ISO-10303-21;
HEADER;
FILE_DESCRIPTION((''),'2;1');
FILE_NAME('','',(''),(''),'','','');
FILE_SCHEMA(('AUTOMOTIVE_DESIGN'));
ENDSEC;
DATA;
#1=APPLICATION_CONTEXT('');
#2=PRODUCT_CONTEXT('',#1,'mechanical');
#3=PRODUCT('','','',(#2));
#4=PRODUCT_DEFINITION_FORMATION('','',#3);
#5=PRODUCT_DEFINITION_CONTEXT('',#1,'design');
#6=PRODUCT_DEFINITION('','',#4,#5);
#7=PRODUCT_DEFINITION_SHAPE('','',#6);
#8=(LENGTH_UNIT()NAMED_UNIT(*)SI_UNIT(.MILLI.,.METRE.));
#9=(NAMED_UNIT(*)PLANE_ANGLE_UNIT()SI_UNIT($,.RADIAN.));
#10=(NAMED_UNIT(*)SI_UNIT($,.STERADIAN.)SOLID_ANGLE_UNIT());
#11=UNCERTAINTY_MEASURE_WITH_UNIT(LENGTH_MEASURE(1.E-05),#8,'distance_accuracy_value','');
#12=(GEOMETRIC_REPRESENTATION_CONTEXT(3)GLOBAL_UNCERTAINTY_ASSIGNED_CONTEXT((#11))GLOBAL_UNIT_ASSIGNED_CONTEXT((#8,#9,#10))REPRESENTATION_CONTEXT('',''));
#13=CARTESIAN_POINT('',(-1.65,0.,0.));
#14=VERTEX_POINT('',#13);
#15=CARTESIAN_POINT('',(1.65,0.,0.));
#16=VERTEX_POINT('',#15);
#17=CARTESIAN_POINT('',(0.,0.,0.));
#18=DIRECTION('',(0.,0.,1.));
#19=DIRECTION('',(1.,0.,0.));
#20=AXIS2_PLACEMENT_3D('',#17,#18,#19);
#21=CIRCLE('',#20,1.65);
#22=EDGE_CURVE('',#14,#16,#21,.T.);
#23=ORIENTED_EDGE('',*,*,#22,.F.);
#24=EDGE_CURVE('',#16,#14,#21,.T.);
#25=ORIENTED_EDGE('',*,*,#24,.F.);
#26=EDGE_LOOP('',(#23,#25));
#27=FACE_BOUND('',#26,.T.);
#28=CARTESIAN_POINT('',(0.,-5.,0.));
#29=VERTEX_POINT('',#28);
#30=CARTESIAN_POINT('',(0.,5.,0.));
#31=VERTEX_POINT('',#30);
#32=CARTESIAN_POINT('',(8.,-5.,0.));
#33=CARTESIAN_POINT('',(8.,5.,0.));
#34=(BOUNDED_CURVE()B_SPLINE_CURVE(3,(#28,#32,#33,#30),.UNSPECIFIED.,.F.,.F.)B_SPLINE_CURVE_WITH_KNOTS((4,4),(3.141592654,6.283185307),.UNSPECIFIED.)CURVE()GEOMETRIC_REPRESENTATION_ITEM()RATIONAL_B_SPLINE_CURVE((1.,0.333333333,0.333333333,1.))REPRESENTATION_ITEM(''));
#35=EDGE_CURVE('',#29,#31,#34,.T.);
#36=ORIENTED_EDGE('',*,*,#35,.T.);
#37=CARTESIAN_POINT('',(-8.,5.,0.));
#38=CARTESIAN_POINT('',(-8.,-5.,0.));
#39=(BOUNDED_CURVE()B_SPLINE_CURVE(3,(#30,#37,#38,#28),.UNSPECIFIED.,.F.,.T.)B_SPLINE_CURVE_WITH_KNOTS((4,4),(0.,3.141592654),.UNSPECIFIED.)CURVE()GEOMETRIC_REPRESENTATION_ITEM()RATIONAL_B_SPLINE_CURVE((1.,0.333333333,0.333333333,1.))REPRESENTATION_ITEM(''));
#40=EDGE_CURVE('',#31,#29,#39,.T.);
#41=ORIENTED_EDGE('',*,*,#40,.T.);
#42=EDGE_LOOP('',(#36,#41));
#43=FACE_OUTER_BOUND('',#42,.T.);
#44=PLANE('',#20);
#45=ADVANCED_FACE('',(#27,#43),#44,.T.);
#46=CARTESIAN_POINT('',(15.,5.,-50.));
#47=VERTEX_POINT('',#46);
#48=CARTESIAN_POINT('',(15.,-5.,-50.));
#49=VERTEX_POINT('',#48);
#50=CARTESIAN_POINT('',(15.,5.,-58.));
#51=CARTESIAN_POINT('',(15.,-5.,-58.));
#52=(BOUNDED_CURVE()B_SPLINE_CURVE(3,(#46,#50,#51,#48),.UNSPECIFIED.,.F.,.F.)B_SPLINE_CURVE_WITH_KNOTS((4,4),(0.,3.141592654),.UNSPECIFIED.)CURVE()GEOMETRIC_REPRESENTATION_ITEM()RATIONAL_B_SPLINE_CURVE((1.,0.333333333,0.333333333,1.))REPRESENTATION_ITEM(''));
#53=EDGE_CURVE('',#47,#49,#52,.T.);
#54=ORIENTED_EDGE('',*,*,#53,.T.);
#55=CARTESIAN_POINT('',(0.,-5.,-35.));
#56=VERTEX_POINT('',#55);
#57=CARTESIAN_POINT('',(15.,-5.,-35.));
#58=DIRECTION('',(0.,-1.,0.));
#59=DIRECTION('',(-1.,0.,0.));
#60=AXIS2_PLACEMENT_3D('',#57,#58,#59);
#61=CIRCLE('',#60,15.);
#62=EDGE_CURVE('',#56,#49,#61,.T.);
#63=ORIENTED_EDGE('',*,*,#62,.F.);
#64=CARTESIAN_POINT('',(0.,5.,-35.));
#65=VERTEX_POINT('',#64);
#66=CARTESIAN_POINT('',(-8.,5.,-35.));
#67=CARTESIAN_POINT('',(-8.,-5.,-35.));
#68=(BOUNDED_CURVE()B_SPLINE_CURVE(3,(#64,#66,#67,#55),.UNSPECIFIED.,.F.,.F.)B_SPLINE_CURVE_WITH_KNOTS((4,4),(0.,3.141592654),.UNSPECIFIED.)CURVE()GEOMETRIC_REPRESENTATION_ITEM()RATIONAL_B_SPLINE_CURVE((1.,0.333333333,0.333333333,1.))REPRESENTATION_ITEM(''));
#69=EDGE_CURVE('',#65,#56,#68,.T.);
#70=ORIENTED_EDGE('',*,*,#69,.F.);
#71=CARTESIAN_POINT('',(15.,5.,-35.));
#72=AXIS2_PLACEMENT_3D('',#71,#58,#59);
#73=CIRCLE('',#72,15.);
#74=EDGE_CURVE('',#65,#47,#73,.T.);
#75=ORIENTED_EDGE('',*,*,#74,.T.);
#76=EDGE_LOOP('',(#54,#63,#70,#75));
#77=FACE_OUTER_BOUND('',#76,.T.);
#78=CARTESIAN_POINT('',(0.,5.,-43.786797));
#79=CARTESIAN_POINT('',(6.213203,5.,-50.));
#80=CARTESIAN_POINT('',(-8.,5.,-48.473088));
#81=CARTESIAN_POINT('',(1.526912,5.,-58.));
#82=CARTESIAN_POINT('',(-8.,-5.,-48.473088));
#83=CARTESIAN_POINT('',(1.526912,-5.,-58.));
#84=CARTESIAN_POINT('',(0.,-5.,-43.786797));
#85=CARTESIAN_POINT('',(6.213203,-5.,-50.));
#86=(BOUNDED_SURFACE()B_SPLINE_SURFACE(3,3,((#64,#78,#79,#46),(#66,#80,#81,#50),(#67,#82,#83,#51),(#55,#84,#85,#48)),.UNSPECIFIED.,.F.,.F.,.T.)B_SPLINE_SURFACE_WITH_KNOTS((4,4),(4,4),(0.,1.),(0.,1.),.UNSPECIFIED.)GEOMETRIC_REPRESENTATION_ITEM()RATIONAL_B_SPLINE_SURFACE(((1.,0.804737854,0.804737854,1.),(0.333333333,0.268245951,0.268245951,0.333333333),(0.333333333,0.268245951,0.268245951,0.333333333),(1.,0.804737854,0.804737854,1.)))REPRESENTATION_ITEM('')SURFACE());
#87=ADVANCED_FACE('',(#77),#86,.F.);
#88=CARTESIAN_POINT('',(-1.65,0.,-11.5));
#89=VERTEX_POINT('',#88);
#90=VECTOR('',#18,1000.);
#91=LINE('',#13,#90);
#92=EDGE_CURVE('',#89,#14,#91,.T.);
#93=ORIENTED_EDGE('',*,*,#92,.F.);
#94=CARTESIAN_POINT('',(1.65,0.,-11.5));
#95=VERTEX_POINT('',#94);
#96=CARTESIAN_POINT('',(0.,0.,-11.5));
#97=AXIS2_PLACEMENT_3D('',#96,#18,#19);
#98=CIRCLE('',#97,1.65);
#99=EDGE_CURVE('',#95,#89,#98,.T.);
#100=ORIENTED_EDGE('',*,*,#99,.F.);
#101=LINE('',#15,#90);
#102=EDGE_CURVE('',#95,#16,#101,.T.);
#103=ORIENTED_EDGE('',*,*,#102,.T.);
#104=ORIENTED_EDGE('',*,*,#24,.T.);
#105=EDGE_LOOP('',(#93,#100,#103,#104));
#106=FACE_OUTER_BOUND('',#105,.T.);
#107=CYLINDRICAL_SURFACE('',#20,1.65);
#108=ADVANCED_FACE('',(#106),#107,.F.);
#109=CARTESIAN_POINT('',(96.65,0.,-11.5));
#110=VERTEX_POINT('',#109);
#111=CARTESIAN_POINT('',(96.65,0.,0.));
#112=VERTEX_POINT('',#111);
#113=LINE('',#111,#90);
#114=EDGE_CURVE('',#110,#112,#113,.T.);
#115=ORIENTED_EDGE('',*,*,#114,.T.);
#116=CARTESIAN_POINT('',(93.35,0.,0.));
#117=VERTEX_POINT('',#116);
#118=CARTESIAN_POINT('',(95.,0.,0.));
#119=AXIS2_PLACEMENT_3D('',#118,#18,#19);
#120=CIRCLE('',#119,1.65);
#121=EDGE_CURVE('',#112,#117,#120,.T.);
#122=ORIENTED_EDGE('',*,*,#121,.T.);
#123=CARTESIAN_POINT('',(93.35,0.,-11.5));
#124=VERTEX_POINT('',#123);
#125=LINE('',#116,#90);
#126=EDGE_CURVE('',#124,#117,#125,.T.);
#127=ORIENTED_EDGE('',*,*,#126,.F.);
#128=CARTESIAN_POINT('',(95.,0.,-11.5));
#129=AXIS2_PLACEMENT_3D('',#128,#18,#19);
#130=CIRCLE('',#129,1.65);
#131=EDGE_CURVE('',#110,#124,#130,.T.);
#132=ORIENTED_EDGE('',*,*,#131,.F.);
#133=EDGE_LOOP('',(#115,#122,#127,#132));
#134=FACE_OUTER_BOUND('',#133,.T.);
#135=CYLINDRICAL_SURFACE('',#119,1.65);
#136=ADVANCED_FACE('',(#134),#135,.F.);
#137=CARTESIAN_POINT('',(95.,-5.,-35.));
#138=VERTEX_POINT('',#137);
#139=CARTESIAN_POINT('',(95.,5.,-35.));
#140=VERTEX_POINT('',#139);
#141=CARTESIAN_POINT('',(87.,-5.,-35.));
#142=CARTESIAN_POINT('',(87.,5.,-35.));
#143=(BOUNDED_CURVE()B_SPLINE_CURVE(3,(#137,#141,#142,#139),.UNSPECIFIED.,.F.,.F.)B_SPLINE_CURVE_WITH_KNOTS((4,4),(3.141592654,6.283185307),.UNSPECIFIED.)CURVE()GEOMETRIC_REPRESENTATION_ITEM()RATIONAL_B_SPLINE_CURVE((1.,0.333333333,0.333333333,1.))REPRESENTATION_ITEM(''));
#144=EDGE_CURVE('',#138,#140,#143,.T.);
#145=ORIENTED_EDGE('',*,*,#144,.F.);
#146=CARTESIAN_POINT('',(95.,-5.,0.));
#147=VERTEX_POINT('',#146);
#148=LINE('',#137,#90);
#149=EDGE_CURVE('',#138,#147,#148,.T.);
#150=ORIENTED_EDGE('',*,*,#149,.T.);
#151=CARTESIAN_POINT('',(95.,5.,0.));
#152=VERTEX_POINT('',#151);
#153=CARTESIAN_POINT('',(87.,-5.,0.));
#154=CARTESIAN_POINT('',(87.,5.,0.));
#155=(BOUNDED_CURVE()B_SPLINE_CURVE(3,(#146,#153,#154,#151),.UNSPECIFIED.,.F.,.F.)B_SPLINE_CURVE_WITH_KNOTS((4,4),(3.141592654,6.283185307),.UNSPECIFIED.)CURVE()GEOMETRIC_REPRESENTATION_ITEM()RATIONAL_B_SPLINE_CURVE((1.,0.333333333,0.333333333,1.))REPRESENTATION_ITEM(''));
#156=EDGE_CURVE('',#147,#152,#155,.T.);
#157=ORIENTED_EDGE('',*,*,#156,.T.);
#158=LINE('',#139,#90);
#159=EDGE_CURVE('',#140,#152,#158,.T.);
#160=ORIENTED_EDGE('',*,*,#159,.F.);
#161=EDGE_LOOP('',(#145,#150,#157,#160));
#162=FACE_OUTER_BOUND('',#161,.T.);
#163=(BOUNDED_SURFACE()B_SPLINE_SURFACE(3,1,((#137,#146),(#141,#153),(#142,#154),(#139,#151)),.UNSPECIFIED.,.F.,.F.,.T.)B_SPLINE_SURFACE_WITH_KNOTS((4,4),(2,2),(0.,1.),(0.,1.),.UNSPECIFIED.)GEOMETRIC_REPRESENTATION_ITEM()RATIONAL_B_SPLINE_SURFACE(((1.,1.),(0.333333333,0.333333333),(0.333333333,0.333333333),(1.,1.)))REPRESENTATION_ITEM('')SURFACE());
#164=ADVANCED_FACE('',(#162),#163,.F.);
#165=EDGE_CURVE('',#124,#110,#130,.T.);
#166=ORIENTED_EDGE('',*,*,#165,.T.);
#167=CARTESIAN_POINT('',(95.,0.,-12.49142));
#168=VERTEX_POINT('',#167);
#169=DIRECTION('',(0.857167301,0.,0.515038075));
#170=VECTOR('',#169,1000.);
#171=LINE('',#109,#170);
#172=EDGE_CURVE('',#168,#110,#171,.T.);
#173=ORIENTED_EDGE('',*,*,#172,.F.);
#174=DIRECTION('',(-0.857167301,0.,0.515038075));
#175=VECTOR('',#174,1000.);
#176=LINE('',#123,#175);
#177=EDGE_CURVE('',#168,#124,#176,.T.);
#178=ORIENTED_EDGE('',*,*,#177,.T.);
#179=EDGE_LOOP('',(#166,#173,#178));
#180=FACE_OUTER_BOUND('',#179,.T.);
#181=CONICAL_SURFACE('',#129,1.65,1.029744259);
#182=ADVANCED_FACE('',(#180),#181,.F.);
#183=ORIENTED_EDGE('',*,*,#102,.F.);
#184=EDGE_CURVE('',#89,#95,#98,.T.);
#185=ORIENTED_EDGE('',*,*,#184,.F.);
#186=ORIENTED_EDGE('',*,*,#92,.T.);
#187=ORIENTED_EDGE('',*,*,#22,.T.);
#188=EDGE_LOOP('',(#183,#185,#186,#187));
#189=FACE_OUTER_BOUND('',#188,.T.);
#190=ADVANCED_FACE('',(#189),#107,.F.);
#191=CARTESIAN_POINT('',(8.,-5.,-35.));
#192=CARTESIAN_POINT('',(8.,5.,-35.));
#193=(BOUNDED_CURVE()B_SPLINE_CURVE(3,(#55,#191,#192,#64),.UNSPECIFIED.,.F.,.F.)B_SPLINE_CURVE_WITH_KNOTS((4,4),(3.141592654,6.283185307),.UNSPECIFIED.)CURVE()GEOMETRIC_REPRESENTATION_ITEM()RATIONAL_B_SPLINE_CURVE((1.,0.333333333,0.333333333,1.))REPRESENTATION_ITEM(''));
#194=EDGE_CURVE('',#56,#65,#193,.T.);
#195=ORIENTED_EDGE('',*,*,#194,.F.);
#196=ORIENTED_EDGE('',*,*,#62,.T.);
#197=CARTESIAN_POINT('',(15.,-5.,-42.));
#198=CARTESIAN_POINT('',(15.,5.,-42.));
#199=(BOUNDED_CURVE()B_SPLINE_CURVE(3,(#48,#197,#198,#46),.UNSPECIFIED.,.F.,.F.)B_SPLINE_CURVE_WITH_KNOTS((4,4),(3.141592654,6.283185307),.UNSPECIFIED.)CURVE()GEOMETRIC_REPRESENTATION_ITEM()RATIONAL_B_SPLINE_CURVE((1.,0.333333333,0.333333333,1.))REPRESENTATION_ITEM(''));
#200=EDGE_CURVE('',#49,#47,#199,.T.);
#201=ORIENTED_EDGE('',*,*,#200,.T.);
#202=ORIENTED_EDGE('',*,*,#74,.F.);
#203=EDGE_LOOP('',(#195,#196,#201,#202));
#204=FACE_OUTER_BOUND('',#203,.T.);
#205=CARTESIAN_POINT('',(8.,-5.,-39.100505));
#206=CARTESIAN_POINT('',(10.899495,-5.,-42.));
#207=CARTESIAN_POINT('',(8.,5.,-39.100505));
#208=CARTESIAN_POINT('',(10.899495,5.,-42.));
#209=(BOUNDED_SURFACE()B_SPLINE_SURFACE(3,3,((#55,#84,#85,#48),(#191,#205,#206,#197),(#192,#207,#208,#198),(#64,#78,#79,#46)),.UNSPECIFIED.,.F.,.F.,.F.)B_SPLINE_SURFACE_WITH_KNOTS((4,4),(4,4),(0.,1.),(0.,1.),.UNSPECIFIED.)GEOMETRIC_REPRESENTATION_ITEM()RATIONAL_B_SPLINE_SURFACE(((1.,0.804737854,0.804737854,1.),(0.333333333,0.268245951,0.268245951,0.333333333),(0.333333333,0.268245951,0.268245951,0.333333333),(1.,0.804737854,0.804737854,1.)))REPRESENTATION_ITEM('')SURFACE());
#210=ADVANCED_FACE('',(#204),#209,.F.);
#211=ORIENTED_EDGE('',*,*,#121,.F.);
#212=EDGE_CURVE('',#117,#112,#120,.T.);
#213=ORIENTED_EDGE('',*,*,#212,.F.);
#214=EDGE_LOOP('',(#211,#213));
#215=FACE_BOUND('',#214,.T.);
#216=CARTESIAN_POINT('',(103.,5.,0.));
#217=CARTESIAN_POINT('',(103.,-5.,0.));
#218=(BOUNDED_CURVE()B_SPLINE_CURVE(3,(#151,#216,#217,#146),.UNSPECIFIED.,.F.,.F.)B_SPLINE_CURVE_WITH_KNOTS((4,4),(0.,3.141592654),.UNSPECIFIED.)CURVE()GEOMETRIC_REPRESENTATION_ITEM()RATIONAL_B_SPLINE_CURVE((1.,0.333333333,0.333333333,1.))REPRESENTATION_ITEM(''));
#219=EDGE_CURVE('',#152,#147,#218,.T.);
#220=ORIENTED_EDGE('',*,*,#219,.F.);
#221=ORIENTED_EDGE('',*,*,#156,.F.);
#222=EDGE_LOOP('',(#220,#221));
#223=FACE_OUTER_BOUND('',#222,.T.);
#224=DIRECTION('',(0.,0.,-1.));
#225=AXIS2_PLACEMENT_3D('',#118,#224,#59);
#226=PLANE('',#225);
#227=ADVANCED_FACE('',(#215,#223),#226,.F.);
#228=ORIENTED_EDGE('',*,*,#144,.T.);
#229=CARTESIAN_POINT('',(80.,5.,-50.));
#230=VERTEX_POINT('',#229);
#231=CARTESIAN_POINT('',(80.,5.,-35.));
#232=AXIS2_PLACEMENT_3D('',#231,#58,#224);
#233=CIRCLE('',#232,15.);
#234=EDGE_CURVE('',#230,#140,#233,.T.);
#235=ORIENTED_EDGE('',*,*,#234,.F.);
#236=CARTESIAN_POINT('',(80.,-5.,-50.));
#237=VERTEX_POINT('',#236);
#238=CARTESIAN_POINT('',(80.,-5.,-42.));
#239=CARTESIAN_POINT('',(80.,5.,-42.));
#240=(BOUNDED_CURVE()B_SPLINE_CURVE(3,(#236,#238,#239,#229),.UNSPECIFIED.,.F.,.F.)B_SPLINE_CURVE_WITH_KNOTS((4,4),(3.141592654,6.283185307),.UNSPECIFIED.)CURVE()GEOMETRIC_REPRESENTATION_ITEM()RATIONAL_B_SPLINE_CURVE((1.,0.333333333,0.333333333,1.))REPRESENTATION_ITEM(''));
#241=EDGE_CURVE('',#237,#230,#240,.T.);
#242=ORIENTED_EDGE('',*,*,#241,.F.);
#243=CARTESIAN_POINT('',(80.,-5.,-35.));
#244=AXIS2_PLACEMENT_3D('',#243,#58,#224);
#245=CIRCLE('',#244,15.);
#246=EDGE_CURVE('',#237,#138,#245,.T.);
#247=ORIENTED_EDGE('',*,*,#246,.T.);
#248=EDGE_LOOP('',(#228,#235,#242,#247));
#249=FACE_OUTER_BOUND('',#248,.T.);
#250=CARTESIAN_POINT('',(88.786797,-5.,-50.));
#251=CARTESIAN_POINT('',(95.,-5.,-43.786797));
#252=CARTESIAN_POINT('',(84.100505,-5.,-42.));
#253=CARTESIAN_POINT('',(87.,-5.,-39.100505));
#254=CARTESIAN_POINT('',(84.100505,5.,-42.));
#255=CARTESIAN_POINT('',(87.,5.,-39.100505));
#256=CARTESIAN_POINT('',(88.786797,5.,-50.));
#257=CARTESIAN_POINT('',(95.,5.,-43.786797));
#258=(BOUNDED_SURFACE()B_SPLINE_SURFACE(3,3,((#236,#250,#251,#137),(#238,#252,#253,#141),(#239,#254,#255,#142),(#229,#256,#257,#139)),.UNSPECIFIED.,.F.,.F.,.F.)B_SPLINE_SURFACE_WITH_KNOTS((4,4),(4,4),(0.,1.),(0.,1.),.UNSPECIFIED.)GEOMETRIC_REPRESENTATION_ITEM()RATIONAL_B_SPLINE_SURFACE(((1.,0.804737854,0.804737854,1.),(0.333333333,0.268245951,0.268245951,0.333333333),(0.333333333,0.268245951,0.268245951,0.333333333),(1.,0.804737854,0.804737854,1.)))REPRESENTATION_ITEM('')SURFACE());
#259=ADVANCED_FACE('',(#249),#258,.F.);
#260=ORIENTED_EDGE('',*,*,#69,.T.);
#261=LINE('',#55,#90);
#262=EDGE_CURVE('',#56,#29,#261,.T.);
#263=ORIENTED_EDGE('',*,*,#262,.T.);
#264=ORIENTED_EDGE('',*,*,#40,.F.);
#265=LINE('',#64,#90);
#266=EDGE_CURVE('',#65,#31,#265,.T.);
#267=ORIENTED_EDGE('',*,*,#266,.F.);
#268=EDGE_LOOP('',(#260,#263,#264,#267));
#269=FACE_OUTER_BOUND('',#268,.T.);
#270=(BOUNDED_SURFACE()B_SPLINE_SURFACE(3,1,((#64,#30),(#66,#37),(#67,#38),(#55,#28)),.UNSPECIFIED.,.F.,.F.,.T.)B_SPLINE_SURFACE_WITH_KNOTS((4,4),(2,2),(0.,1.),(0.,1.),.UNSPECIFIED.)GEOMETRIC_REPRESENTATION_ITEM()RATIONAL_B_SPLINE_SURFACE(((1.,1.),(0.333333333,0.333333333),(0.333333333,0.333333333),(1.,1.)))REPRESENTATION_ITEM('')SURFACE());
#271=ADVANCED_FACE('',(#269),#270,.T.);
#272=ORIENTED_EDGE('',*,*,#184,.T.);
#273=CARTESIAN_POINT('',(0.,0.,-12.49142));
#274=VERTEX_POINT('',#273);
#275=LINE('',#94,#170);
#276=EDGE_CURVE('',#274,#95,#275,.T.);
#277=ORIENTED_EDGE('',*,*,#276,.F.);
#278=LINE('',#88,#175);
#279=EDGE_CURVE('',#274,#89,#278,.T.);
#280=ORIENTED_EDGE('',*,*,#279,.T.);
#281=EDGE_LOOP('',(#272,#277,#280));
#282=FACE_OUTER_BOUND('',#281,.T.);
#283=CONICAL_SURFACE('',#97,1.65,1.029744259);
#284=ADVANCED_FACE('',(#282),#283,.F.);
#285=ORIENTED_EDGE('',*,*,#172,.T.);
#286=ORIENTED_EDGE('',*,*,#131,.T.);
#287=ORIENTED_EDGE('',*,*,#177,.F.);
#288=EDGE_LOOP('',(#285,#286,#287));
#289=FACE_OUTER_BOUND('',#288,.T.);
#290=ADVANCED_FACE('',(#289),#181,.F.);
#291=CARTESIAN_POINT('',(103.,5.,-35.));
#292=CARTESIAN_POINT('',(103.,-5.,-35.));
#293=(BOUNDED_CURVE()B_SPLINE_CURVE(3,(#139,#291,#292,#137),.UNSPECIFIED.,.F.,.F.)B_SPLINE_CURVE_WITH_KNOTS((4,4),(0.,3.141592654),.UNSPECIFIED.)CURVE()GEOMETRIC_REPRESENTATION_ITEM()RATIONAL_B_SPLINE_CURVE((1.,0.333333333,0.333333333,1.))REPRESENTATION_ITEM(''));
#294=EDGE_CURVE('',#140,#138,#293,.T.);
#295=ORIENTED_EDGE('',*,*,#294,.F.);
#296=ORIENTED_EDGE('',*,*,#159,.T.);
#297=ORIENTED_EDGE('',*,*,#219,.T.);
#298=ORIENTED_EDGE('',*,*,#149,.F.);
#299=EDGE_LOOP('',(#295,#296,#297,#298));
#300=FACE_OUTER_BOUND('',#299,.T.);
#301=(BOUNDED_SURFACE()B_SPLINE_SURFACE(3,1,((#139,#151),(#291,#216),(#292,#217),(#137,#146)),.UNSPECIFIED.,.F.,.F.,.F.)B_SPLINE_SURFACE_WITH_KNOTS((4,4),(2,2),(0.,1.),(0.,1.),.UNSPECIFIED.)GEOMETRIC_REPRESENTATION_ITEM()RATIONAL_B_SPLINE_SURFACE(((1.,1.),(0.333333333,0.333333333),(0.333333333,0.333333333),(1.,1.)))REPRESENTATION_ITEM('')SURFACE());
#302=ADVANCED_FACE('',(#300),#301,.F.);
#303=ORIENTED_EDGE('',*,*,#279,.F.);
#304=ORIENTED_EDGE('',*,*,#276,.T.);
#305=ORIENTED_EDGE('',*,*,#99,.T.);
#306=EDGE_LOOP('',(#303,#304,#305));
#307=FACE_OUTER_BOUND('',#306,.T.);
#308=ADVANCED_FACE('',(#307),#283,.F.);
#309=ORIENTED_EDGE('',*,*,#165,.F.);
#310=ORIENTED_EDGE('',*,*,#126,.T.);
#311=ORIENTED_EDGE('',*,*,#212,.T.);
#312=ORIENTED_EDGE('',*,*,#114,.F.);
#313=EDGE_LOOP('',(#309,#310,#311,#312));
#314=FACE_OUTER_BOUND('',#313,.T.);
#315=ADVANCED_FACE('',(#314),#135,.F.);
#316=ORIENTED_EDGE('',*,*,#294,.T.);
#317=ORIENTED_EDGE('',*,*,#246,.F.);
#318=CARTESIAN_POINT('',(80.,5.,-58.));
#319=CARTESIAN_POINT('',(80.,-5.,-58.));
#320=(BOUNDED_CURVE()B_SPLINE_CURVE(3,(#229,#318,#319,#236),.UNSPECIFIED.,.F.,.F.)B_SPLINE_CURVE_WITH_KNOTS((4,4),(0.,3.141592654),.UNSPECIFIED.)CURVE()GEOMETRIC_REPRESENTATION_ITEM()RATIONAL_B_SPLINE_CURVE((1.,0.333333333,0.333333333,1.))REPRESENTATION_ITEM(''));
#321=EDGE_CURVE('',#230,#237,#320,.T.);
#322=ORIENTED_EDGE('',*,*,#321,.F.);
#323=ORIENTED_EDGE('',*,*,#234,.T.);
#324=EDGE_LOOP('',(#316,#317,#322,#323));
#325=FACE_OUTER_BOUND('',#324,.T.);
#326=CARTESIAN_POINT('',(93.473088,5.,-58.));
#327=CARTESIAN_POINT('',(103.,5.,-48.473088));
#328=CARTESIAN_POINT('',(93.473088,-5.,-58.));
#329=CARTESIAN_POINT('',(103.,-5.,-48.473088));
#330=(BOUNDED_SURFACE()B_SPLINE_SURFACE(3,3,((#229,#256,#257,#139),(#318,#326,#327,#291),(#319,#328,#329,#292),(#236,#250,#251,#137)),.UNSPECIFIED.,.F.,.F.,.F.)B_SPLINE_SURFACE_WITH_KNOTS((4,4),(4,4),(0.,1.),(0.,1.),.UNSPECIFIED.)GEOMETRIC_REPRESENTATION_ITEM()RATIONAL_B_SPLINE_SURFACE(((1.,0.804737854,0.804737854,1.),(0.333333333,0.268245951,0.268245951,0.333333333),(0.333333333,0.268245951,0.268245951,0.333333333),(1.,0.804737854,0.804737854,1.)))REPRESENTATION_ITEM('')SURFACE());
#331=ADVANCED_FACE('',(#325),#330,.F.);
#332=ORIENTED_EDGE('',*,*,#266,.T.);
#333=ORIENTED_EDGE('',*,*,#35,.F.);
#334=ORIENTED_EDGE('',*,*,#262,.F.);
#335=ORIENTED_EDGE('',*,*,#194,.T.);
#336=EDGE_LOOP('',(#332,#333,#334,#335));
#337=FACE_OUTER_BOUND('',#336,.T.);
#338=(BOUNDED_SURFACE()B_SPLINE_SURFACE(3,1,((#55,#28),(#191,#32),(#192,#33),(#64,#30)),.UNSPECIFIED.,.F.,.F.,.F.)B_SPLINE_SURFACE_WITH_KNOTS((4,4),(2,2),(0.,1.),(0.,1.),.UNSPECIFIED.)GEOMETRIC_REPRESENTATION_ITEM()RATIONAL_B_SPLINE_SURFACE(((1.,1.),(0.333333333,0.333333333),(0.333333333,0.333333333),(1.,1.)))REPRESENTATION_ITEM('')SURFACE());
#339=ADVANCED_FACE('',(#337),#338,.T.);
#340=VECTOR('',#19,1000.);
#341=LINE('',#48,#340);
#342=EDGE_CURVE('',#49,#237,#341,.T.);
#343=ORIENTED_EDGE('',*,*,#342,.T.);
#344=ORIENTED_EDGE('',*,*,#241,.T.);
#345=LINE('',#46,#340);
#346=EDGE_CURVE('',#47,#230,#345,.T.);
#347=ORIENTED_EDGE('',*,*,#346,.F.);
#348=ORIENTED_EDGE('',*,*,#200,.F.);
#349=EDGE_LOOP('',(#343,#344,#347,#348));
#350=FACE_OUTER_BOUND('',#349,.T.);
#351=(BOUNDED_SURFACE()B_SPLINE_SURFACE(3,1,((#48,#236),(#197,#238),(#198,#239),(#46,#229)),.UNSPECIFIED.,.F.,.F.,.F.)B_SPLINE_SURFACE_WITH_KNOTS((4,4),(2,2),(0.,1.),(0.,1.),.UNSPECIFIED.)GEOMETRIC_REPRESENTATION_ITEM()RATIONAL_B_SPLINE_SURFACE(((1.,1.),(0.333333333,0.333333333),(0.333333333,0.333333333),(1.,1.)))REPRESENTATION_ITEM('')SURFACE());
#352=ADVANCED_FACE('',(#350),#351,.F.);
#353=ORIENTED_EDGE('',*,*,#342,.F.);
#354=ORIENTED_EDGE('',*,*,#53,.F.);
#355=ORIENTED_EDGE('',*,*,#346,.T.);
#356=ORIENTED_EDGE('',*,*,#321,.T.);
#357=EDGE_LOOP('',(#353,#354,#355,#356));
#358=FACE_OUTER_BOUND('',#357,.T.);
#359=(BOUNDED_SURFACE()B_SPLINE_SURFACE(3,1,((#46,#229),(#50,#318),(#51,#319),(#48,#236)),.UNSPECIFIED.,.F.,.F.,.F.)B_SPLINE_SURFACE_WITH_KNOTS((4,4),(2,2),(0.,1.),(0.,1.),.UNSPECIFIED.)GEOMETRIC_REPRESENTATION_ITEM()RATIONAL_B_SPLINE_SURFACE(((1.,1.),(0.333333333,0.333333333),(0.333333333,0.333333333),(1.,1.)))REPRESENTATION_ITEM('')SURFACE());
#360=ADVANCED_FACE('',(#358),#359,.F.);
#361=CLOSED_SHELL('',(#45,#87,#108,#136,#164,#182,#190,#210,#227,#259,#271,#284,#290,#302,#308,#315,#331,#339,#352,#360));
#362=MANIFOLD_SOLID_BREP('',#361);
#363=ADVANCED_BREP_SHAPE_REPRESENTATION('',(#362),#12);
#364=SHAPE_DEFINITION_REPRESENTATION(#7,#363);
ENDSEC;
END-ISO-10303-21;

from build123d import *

# Parameters (mm, degrees)
SKETCH_1_RX            = 5
SKETCH_1_RY            = 4
HOLE_WIZARD_M4_1_D     = 3.3
HOLE_WIZARD_M4_1_DEPTH = 11.5
HOLE_WIZARD_M4_1_TIP   = 0.991420021


with BuildPart() as part:
    # 扫描1: sweep along a path in 草图2
    with BuildLine(Plane(origin=(0, 0, 0), x_dir=(1, 0, 0), z_dir=(0, 1, 0))) as sweep_1_path:
        Line((0, 0), (0, 35))
        ThreePointArc((0, 35), (4.393398282, 45.606601718), (15, 50))
        Line((15, 50), (80, 50))
        ThreePointArc((80, 50), (90.606601718, 45.606601718), (95, 35))
        Line((95, 35), (95, 0))
    # 草图1 → 扫描1 (sweep)
    with BuildSketch(Plane.XY):
        with Locations(Location((0, 0), (0, 0, 90))):
            Ellipse(SKETCH_1_RX, SKETCH_1_RY)
    sweep(path=sweep_1_path.line)

    # M4 螺纹孔1
    with Locations(Plane.XY):
        with Locations((0, 0), (95, 0)):
            Hole(HOLE_WIZARD_M4_1_D / 2, depth=HOLE_WIZARD_M4_1_DEPTH)
            with Locations((0, 0, -(HOLE_WIZARD_M4_1_DEPTH + HOLE_WIZARD_M4_1_TIP / 2))):  # 118° drill point
                Cone(0, HOLE_WIZARD_M4_1_D / 2, HOLE_WIZARD_M4_1_TIP, mode=Mode.SUBTRACT)


solid = part.part
